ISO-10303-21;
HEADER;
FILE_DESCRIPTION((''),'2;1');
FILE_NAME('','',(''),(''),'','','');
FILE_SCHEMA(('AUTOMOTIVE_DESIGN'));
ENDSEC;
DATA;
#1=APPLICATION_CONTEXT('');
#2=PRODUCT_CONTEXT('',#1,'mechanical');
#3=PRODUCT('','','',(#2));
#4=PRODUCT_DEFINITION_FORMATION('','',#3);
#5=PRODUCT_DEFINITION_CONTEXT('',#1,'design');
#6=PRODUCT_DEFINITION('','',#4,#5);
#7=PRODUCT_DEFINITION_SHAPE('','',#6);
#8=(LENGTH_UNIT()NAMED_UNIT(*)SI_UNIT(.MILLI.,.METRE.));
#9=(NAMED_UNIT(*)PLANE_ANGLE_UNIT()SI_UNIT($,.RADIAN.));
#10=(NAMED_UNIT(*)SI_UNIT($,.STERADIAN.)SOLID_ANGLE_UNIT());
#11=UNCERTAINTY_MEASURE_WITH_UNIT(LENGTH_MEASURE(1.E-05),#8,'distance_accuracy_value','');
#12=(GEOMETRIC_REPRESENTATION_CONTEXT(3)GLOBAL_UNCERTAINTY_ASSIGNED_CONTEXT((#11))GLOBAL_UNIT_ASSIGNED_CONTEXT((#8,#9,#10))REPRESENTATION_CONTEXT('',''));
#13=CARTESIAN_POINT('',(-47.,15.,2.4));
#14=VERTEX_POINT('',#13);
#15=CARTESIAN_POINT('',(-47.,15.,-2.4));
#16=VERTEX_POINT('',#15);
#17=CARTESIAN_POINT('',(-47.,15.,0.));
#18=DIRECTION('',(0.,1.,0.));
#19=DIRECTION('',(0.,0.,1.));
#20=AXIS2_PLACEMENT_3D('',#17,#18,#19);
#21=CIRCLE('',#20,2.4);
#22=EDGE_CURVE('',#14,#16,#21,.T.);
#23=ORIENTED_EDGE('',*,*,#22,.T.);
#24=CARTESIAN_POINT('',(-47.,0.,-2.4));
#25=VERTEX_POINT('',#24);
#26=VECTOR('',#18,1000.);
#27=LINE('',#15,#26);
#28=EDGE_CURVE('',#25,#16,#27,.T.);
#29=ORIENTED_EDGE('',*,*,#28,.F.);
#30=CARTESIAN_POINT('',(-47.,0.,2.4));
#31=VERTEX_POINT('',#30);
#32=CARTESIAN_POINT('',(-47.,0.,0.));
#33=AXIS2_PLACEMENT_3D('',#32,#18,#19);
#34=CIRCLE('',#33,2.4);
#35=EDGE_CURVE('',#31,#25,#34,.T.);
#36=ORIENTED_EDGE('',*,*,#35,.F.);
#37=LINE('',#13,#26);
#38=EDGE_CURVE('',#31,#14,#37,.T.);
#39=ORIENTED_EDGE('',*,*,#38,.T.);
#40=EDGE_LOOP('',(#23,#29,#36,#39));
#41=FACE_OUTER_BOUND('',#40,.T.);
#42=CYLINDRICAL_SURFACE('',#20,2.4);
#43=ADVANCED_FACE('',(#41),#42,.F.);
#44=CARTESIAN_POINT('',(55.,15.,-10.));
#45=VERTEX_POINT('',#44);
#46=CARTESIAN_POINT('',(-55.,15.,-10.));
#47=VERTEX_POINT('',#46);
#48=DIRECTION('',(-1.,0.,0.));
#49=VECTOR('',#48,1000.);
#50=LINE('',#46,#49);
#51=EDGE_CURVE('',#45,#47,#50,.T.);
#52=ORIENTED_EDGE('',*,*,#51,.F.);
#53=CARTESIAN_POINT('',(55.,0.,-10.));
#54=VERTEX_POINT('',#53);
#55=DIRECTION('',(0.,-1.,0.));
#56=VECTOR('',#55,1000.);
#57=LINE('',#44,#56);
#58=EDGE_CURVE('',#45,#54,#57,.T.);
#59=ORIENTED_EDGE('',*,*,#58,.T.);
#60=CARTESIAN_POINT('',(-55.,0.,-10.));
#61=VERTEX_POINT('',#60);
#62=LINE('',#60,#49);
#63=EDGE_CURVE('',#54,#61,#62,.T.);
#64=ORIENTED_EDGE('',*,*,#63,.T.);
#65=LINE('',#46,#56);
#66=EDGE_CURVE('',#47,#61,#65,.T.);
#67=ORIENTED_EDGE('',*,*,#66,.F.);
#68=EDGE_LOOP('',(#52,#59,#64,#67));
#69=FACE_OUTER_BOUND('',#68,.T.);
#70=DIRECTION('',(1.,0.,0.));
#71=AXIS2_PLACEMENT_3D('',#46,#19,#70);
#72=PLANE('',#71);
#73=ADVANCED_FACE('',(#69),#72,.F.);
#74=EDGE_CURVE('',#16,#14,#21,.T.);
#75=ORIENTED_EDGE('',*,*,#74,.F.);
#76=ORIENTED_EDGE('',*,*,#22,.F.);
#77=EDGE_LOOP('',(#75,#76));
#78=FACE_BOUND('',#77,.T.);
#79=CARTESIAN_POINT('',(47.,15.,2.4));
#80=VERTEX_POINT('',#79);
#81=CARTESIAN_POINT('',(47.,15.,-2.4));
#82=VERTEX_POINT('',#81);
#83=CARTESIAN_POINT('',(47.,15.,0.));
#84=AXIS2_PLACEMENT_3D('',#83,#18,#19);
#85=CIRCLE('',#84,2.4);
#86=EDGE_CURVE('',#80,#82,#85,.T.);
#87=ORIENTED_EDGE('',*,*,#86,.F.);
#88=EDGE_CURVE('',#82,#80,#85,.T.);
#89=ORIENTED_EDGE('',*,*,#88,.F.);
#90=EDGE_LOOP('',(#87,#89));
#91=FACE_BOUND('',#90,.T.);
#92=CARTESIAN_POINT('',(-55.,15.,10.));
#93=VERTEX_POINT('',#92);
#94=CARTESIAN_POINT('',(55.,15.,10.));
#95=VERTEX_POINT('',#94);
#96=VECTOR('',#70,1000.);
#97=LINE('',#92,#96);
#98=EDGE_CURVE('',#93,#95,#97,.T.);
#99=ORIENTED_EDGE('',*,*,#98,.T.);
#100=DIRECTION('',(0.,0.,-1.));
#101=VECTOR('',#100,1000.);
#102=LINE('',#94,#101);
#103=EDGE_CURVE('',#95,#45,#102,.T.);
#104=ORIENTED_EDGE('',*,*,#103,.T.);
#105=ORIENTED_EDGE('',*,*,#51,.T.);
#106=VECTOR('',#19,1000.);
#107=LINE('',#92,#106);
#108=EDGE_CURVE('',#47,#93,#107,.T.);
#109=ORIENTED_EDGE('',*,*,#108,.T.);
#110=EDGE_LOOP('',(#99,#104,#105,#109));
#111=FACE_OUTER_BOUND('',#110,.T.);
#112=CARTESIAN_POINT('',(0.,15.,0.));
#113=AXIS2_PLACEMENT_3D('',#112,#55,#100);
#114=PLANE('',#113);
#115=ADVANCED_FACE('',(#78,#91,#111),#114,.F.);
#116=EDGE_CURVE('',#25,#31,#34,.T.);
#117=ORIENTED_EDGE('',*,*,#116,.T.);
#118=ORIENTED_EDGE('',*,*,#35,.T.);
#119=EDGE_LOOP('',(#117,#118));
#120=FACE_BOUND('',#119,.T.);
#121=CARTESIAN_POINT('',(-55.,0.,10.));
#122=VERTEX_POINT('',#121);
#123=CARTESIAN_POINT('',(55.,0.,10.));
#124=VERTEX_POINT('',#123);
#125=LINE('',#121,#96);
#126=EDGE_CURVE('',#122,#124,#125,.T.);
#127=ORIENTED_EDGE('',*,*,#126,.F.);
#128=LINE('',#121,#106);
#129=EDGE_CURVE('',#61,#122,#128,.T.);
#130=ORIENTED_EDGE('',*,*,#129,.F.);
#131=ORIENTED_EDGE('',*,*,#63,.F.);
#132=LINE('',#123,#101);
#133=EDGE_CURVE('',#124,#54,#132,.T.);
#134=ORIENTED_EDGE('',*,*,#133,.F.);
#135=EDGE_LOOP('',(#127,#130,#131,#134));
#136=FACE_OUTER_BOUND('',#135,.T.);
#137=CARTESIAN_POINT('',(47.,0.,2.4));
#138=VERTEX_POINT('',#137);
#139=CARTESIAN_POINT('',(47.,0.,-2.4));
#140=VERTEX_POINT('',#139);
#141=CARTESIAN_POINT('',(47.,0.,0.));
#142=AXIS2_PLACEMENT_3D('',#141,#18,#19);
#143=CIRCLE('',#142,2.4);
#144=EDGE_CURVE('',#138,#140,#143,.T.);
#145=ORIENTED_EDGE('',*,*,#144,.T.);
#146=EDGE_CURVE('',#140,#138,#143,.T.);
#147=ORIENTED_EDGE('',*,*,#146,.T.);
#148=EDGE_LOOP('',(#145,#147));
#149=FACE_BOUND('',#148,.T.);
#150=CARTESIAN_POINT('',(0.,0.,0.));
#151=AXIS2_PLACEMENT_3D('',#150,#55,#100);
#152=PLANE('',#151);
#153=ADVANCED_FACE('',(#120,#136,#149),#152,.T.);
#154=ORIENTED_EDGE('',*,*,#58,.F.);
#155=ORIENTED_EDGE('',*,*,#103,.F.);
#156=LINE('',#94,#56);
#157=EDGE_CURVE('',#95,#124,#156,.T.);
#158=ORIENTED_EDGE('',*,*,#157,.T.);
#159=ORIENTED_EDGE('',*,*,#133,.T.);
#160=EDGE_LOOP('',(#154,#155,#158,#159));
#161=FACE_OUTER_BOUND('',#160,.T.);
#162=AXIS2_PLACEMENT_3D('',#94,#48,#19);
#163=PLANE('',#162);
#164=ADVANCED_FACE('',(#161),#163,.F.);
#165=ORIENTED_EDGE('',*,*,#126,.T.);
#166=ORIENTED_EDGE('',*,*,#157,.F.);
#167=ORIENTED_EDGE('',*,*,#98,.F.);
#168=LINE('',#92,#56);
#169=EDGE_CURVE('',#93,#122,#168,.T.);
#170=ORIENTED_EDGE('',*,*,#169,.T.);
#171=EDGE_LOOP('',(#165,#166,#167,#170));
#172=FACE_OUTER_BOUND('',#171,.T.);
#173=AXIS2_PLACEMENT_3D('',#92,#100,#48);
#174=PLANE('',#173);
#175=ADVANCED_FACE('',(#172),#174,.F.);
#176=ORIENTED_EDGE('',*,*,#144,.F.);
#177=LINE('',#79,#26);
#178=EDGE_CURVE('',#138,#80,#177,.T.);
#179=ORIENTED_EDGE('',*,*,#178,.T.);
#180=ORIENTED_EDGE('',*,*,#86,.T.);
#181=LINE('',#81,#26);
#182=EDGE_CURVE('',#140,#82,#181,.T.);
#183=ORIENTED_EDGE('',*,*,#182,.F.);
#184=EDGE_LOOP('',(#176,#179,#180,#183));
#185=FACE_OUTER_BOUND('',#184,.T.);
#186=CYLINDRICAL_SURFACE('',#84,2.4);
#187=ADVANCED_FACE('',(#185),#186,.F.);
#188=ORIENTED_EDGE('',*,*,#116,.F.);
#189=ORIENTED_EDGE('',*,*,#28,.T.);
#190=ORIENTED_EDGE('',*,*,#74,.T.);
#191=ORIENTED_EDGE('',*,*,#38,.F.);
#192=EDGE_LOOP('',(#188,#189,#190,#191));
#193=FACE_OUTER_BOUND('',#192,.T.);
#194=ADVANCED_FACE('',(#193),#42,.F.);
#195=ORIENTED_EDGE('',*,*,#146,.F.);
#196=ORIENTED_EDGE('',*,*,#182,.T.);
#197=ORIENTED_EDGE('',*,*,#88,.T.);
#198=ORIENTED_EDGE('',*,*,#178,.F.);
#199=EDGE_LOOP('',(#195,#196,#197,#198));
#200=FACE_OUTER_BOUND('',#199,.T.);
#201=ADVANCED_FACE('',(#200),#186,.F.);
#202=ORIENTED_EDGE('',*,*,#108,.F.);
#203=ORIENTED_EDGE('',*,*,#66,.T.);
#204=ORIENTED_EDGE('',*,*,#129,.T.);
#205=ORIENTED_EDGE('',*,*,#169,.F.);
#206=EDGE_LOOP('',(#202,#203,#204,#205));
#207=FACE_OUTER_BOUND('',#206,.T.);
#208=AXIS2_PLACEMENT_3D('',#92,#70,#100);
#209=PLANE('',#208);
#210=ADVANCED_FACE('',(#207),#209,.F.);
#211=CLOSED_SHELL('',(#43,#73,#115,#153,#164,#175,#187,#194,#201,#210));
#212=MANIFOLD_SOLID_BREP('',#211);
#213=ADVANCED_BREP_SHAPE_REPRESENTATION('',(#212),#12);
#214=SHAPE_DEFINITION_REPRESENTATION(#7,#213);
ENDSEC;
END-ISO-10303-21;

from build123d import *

# Parameters (mm, degrees)
SKETCH_1_W         = 110
SKETCH_1_H         = 20
EXTRUDE_1_DEPTH    = 15
HOLE_WIZARD_M4_1_D = 4.8


with BuildPart() as part:
    # 草图1 → 凸台-拉伸1 (new body)
    with BuildSketch(Plane(origin=(0, 0, 0), x_dir=(1, 0, 0), z_dir=(0, 1, 0))):
        Rectangle(SKETCH_1_W, SKETCH_1_H)
    extrude(amount=EXTRUDE_1_DEPTH)

    # M4 间隙孔1 (through all)
    with Locations(Plane(origin=(0, 15, 0), x_dir=(1, 0, 0), z_dir=(0, 1, 0))):
        with Locations((-47, 0), (47, 0)):
            Hole(HOLE_WIZARD_M4_1_D / 2)


solid = part.part
